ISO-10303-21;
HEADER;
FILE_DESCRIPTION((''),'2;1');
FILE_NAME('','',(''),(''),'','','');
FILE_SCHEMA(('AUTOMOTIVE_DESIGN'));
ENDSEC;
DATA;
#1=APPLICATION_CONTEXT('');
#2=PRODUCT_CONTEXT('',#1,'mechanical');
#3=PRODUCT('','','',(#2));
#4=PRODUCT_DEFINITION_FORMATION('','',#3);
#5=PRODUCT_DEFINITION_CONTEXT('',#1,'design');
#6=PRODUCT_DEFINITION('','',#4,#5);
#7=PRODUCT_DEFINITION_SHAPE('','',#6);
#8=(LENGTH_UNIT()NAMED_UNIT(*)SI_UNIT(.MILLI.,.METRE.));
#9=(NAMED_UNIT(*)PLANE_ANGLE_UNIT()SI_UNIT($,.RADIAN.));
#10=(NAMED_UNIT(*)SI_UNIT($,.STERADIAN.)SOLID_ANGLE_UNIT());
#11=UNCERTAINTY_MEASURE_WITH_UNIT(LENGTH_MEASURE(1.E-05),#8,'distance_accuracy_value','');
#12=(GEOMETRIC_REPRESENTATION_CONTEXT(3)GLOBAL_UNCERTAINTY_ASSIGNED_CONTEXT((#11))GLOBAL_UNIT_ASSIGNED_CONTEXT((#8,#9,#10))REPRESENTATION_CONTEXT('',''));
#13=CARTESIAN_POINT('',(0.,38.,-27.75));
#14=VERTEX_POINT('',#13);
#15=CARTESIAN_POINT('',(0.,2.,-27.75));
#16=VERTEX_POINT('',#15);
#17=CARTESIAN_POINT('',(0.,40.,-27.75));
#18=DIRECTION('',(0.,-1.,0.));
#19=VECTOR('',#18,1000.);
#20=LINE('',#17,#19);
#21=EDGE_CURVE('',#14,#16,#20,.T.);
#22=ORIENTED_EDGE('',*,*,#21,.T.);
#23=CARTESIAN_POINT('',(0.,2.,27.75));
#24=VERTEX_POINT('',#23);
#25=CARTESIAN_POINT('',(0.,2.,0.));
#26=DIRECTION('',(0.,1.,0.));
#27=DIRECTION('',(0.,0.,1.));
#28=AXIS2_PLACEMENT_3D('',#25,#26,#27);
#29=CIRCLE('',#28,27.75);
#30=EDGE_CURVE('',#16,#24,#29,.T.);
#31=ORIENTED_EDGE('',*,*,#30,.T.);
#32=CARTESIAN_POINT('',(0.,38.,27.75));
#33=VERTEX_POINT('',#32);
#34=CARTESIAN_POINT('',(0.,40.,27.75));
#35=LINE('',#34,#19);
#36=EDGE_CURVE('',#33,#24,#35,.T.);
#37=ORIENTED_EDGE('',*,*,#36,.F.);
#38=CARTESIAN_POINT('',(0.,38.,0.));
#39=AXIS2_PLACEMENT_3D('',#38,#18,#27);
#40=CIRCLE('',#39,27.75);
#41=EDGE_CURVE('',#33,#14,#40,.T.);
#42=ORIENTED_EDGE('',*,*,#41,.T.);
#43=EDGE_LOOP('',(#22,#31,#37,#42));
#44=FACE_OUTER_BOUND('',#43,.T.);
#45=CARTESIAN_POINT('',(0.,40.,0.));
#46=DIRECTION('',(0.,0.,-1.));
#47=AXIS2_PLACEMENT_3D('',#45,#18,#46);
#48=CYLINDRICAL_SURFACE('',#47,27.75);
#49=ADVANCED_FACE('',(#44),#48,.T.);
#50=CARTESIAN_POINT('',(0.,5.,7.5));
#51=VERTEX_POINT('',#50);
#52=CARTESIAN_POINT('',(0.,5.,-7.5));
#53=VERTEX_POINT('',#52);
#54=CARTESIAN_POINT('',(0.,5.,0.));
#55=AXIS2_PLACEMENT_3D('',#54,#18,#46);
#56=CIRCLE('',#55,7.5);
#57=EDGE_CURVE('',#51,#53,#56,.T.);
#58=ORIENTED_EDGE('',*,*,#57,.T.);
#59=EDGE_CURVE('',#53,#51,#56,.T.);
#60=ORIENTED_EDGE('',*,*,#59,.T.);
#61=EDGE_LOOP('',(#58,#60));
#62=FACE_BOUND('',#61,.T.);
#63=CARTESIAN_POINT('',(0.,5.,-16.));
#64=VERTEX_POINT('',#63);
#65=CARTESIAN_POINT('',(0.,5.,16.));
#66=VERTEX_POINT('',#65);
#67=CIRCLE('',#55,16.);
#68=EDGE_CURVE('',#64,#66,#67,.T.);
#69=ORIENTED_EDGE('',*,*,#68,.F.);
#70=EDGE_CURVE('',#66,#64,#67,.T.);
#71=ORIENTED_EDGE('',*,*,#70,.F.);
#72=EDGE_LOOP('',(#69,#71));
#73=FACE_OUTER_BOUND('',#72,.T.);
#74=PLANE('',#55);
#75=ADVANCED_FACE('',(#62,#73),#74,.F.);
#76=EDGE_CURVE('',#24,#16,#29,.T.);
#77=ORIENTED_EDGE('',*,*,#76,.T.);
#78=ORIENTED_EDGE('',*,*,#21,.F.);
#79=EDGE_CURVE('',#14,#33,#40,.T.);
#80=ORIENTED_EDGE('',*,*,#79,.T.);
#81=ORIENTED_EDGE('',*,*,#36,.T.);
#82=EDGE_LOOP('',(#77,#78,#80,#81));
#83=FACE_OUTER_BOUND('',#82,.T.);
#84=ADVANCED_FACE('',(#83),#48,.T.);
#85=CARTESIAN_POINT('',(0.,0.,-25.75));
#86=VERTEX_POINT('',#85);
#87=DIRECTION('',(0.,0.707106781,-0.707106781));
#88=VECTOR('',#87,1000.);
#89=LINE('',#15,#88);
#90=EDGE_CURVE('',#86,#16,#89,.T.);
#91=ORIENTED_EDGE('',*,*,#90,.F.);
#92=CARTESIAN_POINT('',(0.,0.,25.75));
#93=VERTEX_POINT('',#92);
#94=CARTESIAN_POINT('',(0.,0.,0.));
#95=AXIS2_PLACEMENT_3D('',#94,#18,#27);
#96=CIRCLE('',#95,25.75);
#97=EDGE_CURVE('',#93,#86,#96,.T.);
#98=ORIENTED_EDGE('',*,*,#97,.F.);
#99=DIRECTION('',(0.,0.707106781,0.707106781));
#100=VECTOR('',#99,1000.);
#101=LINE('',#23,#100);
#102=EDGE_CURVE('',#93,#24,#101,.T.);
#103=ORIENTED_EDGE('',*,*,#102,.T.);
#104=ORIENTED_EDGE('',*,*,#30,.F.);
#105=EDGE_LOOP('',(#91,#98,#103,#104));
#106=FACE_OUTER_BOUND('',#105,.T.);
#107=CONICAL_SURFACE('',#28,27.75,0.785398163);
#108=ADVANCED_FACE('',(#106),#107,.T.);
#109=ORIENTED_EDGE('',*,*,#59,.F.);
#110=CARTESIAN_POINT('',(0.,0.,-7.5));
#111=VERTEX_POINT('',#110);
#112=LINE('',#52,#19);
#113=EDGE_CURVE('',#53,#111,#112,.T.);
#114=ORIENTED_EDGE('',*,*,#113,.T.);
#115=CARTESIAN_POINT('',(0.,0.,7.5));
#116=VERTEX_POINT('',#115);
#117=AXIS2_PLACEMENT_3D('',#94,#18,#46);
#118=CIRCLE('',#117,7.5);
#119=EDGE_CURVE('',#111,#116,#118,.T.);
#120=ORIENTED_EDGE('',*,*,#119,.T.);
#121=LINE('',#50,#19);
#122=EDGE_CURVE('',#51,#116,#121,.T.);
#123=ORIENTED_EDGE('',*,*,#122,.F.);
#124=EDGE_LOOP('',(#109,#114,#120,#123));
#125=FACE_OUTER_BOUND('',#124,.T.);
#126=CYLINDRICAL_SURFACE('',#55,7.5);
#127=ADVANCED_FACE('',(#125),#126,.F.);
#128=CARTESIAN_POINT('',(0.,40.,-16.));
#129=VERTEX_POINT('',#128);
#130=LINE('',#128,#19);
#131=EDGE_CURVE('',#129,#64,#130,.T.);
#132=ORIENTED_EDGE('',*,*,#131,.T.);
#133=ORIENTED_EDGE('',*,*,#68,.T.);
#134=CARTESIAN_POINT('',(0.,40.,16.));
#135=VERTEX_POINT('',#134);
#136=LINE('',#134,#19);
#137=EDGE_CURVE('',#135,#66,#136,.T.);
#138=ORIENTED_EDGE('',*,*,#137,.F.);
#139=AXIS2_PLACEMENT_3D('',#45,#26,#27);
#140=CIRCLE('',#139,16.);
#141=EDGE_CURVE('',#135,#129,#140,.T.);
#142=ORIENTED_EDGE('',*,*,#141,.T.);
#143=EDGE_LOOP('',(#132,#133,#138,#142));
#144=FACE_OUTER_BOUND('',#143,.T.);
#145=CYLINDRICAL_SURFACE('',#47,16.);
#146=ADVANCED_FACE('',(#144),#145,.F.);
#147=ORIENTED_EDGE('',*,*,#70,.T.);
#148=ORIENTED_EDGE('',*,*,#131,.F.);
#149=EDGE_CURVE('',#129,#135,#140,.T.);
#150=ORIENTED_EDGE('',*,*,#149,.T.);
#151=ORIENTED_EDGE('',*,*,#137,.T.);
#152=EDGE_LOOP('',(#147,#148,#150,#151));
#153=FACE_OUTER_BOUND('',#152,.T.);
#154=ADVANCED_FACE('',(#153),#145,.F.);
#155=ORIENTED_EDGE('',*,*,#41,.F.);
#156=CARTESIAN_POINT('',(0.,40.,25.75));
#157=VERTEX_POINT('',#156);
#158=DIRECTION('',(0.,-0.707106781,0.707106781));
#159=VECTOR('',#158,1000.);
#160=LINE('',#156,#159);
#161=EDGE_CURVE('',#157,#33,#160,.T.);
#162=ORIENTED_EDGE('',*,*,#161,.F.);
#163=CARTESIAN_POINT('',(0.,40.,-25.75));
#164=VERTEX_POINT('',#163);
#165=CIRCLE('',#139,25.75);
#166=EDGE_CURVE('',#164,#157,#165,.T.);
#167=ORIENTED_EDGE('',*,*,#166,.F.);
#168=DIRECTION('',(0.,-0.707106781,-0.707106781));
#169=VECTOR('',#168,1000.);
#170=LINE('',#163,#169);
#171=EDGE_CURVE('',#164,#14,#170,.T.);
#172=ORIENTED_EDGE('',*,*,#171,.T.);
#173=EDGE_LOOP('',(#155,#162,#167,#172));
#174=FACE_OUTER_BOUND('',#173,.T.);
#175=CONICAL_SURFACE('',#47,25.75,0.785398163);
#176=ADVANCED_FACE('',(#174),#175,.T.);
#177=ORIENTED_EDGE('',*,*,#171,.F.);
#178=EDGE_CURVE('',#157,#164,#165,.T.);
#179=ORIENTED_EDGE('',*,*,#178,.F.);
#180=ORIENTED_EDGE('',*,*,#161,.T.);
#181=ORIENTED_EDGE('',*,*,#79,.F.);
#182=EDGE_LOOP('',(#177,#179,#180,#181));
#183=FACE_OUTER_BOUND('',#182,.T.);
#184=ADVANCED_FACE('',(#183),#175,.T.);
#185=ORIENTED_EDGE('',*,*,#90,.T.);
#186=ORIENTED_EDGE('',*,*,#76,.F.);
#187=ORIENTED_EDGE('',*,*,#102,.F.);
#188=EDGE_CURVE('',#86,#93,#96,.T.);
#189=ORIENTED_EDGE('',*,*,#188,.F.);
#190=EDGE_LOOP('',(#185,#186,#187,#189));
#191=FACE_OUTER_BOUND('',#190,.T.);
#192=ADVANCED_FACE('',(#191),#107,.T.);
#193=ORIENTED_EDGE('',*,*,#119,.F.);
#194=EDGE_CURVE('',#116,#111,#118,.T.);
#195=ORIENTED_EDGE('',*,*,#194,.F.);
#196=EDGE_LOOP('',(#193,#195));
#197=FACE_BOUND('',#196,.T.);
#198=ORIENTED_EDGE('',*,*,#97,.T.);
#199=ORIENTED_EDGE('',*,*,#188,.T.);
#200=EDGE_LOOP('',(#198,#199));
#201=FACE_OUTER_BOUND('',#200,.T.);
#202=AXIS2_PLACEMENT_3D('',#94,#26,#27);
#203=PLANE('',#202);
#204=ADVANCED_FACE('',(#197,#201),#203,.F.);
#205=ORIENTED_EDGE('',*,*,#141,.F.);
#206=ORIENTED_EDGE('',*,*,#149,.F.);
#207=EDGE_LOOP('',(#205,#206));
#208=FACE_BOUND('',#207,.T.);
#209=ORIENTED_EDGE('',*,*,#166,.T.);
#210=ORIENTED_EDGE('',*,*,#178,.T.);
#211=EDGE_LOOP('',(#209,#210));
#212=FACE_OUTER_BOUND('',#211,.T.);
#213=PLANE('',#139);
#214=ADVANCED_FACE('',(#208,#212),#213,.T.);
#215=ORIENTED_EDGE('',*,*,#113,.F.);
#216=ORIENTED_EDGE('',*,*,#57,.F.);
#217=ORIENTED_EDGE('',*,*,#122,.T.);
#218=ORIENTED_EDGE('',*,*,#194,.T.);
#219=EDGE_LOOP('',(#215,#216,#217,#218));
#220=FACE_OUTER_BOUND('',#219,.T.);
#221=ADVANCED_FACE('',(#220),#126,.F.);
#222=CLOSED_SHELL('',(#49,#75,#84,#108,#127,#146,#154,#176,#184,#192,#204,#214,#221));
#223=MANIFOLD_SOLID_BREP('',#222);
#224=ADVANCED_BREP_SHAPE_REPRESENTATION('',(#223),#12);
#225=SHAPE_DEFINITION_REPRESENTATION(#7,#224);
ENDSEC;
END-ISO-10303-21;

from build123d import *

# Parameters (mm, degrees)
SKETCH_1_R      = 27.75
SKETCH_1_R_2    = 16
EXTRUDE_1_DEPTH = 40
CHAMFER_1_SIZE  = 2
SKETCH_2_R      = 16
SKETCH_2_R_2    = 7.5
EXTRUDE_2_DEPTH = 5


with BuildPart() as part:
    # 草图1 → 凸台-拉伸1 (new body)
    with BuildSketch(Plane(origin=(0, 0, 0), x_dir=(1, 0, 0), z_dir=(0, 1, 0))):
        with Locations(Location((0, 0, 0), (0, 0, 270))):
            Circle(SKETCH_1_R)
        with Locations(Location((0, 0, 0), (0, 0, 270))):
            Circle(SKETCH_1_R_2, mode=Mode.SUBTRACT)
    extrude(amount=EXTRUDE_1_DEPTH)

    # 倒角1
    chamfer_1_edges = [part.edges().sort_by_distance(p)[0] for p in [
        (0, 0, -27.75),
        (0, 40, -27.75),
    ]]
    chamfer(chamfer_1_edges, length=CHAMFER_1_SIZE)

    # 草图2 → 凸台-拉伸2 (add)
    with BuildSketch(Plane.XZ):
        with Locations(Location((0, 0, 0), (0, 0, 270))):
            Circle(SKETCH_2_R)
        with Locations(Location((0, 0, 0), (0, 0, 270))):
            Circle(SKETCH_2_R_2, mode=Mode.SUBTRACT)
    extrude(amount=-EXTRUDE_2_DEPTH)


solid = part.part
